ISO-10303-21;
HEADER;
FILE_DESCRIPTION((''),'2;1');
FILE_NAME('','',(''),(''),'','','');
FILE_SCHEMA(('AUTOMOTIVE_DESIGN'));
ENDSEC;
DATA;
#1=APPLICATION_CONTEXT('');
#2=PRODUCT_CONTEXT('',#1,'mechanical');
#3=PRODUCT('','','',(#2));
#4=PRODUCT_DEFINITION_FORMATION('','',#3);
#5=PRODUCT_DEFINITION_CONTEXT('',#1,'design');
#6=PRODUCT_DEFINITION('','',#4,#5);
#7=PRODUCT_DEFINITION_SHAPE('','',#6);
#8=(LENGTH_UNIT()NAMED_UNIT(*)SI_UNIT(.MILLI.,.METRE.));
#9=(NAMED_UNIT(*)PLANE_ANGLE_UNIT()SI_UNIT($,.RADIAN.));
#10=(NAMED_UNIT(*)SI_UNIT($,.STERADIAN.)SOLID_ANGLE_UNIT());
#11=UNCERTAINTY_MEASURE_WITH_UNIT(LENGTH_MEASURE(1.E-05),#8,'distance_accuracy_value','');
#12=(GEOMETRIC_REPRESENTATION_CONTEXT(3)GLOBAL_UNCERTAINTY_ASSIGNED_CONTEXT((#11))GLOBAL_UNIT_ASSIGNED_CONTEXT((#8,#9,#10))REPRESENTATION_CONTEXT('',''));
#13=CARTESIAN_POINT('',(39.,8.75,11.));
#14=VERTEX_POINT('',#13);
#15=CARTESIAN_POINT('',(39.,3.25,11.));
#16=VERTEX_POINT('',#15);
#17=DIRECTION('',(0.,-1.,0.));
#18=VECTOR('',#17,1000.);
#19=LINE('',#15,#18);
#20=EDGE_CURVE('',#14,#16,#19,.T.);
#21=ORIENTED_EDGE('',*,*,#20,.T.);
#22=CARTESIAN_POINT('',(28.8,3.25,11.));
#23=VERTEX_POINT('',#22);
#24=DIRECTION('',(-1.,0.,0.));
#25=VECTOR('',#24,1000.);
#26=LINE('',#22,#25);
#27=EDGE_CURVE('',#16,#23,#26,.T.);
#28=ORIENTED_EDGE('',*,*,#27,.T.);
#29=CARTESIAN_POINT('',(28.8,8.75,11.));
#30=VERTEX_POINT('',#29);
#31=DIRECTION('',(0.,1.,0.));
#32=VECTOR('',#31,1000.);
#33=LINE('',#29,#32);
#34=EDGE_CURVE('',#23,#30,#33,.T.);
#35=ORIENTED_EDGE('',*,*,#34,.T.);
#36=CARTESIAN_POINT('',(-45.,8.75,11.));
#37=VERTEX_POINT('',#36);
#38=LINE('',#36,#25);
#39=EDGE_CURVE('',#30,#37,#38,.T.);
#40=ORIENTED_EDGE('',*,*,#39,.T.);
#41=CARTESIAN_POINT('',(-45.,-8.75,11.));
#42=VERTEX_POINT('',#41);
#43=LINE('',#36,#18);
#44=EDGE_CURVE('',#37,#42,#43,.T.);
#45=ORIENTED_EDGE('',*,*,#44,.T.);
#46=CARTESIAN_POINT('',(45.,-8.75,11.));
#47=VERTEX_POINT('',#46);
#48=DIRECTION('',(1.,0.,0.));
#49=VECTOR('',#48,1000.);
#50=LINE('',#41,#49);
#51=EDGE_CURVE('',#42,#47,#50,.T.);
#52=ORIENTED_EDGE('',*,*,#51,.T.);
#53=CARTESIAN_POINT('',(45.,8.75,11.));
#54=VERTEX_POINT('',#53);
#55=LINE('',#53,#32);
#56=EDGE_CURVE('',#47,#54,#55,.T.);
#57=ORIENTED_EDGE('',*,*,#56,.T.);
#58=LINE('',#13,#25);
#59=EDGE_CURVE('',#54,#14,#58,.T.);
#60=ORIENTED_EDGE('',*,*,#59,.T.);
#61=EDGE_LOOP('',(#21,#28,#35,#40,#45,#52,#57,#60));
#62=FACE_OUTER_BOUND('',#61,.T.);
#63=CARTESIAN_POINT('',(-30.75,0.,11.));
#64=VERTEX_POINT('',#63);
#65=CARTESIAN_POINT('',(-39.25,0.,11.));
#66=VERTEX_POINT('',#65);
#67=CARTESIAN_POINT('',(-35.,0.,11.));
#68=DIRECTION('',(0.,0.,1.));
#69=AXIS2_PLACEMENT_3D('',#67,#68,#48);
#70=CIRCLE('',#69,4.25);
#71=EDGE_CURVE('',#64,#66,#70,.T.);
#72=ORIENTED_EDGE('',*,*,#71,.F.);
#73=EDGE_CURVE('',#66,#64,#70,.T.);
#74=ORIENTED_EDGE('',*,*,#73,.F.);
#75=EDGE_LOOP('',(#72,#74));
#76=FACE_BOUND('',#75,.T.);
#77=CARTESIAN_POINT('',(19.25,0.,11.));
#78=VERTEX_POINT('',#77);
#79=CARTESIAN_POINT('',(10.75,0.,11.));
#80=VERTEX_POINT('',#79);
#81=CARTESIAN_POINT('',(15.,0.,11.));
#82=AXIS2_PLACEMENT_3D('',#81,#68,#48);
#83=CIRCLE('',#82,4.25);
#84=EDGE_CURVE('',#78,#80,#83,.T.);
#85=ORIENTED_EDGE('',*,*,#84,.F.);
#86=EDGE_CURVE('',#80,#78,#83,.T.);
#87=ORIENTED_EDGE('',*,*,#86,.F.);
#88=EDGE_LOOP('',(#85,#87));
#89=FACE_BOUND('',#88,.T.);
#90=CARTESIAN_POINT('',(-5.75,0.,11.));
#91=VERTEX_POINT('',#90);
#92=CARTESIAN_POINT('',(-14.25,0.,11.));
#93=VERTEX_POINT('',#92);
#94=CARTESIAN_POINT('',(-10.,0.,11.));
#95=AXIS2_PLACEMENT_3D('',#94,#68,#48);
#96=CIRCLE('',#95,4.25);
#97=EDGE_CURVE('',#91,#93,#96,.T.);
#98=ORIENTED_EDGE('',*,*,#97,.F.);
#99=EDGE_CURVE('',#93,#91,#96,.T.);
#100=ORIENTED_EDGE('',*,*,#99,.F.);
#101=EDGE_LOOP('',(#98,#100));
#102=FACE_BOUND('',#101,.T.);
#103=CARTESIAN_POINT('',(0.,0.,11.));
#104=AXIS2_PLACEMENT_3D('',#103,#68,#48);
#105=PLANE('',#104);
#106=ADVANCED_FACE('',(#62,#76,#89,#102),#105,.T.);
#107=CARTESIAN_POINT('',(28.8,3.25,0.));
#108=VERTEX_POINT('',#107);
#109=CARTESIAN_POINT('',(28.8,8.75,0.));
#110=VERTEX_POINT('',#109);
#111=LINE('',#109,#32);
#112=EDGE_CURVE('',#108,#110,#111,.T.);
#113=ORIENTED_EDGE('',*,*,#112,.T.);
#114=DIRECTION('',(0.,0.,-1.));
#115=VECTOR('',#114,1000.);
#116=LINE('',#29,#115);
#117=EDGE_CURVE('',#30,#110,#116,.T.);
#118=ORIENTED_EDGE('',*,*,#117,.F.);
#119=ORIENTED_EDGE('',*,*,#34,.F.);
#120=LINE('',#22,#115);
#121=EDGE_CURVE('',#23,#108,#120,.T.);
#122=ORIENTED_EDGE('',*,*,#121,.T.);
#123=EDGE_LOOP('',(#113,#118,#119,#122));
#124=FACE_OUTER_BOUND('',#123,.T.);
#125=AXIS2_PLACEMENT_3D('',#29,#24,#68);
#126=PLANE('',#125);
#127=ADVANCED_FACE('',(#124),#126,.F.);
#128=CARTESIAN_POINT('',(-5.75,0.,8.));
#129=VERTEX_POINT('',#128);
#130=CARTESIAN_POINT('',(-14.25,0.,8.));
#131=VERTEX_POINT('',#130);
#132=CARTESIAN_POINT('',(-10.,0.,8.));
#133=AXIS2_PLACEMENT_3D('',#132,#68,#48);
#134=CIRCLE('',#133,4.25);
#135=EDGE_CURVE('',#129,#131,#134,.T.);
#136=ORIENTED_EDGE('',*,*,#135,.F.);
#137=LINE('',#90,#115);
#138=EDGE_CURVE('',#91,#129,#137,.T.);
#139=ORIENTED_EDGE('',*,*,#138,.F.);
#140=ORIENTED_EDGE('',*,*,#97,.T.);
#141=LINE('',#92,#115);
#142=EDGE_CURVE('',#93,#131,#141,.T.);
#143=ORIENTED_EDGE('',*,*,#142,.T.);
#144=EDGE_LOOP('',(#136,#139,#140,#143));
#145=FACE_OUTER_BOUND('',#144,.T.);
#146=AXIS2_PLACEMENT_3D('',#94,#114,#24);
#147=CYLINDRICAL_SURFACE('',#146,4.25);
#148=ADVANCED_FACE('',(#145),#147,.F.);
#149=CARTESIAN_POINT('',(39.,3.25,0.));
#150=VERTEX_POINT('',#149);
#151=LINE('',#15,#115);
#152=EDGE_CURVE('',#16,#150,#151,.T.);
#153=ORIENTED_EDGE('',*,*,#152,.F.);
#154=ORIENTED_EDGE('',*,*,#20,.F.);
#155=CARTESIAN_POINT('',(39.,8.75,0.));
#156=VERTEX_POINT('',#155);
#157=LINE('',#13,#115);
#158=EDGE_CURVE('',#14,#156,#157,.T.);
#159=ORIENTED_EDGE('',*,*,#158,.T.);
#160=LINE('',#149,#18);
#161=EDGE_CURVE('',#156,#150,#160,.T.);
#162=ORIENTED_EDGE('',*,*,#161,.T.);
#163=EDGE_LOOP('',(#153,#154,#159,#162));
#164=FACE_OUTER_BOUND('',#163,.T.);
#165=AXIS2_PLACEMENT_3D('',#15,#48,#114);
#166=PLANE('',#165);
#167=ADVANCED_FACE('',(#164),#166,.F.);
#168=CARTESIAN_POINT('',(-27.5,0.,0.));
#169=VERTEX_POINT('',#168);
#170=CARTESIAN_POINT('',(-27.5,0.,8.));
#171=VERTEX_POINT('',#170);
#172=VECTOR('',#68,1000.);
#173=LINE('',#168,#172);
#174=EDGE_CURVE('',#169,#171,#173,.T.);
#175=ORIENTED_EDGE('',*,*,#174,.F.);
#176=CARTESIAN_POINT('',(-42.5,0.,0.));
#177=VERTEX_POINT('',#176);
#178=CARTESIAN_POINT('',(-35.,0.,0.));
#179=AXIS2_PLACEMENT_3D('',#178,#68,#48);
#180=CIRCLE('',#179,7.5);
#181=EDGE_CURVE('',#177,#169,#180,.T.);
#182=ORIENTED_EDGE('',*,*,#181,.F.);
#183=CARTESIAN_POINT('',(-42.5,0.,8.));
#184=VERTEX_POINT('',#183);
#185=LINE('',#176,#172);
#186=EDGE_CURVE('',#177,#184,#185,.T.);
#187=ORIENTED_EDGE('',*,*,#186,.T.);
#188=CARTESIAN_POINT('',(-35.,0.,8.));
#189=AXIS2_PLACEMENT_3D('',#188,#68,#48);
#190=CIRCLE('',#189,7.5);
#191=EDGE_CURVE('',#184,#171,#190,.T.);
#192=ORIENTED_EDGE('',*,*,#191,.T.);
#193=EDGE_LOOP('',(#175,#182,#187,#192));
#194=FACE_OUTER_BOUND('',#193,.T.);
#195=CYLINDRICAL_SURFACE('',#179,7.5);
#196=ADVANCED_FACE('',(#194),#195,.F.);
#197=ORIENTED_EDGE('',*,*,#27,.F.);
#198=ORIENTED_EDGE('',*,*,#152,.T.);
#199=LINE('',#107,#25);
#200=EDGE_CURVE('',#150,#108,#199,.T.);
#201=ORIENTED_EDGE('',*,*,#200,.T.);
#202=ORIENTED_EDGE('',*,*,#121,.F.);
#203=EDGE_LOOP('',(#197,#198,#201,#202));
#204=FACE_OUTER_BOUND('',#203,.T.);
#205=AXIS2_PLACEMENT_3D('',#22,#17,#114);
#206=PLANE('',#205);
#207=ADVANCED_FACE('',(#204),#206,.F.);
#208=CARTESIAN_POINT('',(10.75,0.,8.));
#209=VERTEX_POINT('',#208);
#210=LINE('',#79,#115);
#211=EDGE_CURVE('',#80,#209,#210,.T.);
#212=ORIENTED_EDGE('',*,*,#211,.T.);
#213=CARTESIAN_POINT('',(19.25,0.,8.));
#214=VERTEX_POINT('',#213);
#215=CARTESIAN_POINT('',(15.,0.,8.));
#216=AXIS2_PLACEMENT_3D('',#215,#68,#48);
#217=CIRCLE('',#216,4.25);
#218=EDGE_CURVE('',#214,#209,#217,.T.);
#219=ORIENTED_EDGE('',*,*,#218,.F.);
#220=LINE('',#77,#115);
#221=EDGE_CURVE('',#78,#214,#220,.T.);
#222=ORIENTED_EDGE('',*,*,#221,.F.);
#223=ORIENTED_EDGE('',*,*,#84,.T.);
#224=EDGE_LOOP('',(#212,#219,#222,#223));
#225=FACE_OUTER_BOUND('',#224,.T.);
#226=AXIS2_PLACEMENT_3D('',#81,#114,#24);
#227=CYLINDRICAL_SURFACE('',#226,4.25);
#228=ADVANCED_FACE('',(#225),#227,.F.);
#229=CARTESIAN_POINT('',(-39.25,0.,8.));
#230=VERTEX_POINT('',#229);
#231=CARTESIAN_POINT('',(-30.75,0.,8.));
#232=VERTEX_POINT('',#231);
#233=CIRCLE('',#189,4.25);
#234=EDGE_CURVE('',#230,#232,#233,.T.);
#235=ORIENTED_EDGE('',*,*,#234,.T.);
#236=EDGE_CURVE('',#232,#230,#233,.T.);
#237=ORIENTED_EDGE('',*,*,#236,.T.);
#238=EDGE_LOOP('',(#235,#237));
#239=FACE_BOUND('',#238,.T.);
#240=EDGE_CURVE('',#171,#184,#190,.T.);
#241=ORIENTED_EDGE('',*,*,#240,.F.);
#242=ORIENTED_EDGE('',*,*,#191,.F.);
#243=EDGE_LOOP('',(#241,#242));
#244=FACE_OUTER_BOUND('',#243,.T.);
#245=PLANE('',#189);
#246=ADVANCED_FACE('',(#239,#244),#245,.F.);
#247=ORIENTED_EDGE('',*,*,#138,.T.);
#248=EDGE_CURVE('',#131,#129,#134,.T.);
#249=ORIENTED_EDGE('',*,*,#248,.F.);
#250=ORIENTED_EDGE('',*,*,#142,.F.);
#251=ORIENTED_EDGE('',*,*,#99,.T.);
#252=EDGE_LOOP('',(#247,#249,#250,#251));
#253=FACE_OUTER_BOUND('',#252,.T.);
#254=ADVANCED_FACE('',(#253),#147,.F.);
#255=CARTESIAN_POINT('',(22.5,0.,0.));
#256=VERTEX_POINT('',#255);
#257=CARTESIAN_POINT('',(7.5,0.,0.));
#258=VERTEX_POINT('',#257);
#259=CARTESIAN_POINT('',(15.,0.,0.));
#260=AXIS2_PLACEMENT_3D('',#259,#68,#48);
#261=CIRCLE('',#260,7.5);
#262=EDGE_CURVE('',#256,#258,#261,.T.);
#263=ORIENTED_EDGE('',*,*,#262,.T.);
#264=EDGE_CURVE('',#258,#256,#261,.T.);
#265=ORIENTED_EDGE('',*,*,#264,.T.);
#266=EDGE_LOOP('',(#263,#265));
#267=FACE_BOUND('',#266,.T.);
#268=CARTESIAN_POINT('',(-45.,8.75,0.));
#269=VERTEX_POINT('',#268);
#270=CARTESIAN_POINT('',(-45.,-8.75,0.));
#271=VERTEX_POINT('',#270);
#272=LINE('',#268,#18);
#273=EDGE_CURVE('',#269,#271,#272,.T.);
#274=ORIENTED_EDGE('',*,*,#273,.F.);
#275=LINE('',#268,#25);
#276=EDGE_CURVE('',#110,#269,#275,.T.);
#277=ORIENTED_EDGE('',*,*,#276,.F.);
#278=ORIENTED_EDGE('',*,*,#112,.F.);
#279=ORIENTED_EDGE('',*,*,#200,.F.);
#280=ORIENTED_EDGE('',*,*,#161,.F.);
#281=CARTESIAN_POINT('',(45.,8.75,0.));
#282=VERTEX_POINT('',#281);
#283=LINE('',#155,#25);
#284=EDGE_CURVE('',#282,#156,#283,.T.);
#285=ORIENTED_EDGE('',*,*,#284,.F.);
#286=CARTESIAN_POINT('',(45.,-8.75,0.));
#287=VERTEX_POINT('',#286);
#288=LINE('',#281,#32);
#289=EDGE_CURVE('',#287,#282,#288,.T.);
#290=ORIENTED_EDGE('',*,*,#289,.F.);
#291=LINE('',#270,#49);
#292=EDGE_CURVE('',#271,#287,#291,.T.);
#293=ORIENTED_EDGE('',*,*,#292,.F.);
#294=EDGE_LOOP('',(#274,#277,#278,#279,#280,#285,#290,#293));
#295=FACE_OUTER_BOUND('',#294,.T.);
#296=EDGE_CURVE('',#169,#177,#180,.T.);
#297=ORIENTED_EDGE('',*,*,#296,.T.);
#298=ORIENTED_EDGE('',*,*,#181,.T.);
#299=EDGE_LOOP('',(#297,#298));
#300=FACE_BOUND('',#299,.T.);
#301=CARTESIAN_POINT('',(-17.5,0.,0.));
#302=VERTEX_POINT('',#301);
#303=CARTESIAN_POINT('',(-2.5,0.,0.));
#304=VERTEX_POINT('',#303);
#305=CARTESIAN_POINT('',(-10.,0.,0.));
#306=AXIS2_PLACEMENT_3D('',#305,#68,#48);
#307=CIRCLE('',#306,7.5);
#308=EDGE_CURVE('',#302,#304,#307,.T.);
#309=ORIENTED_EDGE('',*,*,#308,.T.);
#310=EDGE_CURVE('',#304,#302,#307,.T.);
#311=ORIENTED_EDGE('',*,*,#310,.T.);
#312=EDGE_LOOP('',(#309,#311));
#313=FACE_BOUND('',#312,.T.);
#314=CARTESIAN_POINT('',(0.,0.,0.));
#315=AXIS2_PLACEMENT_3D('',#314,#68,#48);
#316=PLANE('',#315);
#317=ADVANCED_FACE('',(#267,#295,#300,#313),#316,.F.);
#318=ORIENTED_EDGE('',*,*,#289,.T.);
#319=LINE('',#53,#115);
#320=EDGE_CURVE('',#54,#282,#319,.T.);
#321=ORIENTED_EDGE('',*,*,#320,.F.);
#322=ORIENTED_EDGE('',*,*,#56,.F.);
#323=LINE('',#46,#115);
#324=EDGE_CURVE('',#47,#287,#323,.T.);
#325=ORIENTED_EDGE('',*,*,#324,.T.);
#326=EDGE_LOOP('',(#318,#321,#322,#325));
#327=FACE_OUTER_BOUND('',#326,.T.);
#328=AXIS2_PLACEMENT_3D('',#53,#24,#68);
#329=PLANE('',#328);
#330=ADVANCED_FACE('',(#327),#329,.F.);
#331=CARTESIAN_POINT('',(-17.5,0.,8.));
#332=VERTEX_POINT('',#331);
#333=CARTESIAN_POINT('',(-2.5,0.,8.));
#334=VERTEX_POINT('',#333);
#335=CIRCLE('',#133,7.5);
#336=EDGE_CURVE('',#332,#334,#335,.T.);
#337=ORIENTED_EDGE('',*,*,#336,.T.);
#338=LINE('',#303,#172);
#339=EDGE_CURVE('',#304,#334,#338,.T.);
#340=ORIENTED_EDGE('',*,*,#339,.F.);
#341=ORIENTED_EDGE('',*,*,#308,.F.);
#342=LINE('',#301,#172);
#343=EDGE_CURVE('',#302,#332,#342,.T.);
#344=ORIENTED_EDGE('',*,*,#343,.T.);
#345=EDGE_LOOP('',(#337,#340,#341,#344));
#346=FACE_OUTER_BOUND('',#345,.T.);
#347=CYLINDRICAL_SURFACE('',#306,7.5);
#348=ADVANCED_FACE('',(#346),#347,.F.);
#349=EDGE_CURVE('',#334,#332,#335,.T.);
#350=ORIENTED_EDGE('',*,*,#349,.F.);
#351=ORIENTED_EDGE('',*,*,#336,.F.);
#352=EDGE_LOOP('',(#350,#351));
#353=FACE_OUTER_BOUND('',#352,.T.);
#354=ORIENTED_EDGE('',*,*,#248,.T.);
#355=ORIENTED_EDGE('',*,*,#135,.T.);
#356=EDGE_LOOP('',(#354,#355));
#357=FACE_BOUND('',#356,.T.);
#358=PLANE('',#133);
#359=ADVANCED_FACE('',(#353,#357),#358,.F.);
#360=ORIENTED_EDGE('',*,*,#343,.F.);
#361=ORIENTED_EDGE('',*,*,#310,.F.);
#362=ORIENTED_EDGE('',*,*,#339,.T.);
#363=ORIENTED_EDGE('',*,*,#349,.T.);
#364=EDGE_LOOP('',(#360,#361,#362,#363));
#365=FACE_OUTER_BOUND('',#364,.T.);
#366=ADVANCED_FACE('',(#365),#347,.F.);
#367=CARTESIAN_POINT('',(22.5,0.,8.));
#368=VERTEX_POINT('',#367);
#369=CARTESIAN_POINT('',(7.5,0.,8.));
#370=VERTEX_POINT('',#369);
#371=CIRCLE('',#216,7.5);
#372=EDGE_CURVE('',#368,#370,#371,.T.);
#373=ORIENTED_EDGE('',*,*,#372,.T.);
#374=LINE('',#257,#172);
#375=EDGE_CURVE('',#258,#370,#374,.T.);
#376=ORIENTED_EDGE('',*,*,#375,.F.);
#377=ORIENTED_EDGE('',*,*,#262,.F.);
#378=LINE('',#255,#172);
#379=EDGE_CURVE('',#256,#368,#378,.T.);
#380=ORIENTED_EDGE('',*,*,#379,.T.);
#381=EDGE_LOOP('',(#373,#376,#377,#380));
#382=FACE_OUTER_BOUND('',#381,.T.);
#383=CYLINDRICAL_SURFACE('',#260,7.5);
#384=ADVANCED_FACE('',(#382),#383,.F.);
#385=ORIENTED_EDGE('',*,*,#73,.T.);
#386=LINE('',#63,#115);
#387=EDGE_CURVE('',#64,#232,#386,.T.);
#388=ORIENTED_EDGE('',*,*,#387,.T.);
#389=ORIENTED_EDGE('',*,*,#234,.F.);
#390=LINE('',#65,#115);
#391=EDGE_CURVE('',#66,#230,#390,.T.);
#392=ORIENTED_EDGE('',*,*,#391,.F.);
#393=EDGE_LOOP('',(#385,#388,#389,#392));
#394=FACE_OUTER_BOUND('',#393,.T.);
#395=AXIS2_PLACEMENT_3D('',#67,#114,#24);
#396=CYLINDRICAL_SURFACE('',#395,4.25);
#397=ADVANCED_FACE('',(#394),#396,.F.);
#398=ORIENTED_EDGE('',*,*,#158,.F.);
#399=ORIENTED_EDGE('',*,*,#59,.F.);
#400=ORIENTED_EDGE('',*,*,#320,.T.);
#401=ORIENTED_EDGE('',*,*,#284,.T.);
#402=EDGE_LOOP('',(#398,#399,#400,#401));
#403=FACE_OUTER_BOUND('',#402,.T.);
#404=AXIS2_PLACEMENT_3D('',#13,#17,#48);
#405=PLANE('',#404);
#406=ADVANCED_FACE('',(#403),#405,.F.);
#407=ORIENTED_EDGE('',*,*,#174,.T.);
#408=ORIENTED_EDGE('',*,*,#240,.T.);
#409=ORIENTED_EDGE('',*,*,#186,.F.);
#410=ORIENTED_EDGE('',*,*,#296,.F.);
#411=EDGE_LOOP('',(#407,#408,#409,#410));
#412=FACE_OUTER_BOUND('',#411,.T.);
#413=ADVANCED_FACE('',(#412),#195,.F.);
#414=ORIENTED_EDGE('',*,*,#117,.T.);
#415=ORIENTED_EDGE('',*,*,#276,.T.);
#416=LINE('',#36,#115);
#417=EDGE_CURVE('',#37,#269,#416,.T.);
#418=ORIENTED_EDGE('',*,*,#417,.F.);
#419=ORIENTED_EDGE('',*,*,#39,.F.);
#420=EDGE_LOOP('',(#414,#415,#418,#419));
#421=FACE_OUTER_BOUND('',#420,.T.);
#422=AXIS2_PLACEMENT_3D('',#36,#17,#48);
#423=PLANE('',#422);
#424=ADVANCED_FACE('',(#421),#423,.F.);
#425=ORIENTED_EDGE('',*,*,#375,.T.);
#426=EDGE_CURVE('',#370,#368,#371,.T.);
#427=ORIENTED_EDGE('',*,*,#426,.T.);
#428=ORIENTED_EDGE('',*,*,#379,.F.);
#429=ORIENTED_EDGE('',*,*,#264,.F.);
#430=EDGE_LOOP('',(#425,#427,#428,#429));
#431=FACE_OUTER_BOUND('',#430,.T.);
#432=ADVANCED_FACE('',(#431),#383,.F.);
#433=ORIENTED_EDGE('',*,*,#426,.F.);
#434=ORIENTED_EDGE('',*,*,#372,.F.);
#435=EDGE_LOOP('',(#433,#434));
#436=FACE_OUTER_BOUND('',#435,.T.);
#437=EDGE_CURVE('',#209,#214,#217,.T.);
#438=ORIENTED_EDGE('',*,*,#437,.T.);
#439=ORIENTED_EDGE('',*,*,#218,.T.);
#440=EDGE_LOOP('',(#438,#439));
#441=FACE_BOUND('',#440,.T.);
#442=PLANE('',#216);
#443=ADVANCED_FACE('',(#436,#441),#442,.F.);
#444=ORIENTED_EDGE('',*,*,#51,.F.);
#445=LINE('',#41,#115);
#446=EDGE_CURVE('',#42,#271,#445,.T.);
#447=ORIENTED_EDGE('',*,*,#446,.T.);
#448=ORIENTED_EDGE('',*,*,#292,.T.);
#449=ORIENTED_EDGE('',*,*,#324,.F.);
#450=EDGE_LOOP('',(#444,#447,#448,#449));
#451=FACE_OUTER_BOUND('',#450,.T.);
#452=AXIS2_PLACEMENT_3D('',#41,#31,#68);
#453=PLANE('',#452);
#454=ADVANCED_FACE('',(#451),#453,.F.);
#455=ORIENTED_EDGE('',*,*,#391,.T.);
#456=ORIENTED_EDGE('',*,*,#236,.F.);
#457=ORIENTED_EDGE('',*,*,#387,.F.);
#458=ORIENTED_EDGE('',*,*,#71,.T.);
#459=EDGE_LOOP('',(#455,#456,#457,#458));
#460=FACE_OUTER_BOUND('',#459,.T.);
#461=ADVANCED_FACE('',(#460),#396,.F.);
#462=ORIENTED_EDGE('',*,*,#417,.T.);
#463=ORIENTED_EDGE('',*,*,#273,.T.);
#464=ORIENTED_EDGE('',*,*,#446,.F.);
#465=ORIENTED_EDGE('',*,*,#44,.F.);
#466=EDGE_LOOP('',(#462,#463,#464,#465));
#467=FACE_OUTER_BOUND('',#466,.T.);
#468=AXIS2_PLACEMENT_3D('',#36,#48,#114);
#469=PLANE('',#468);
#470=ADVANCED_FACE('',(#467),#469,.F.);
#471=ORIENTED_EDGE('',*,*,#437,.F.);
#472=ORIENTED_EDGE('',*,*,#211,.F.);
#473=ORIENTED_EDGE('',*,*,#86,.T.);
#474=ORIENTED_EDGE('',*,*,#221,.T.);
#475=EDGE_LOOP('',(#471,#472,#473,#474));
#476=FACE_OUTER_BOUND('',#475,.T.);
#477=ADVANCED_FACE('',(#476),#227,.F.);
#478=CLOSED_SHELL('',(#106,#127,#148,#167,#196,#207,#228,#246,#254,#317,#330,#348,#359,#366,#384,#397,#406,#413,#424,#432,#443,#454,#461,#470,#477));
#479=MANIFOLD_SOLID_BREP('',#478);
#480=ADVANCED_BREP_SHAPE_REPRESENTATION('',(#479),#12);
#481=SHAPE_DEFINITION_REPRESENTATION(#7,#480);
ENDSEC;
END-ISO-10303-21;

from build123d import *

# Parameters (mm, degrees)
SKETCH1_R           = 4.25
BOSS_EXTRUDE1_DEPTH = 11
CUT_EXTRUDE1_START  = -3
SKETCH2_R           = 7.5
CUT_EXTRUDE1_DEPTH  = 8


with BuildPart() as part:
    # Sketch1 → Boss-Extrude1 (new body)
    with BuildSketch(Plane.XY):
        Polygon((-45, 8.75), (28.8, 8.75), (28.8, 3.25), (39, 3.25), (39, 8.75), (45, 8.75), (45, -8.75), (-45, -8.75), align=None)
        with Locations((-35, 0)):
            Circle(SKETCH1_R, mode=Mode.SUBTRACT)
        with Locations((-10, 0)):
            Circle(SKETCH1_R, mode=Mode.SUBTRACT)
        with Locations((15, 0)):
            Circle(SKETCH1_R, mode=Mode.SUBTRACT)
    extrude(amount=BOSS_EXTRUDE1_DEPTH)

    # Sketch2 → Cut-Extrude1 (cut)
    with BuildSketch(Plane.XY.offset(11).offset(CUT_EXTRUDE1_START)):
        with Locations((-35, 0)):
            Circle(SKETCH2_R)
        with Locations((-10, 0)):
            Circle(SKETCH2_R)
        with Locations((15, 0)):
            Circle(SKETCH2_R)
    extrude(amount=-CUT_EXTRUDE1_DEPTH, mode=Mode.SUBTRACT)


solid = part.part
